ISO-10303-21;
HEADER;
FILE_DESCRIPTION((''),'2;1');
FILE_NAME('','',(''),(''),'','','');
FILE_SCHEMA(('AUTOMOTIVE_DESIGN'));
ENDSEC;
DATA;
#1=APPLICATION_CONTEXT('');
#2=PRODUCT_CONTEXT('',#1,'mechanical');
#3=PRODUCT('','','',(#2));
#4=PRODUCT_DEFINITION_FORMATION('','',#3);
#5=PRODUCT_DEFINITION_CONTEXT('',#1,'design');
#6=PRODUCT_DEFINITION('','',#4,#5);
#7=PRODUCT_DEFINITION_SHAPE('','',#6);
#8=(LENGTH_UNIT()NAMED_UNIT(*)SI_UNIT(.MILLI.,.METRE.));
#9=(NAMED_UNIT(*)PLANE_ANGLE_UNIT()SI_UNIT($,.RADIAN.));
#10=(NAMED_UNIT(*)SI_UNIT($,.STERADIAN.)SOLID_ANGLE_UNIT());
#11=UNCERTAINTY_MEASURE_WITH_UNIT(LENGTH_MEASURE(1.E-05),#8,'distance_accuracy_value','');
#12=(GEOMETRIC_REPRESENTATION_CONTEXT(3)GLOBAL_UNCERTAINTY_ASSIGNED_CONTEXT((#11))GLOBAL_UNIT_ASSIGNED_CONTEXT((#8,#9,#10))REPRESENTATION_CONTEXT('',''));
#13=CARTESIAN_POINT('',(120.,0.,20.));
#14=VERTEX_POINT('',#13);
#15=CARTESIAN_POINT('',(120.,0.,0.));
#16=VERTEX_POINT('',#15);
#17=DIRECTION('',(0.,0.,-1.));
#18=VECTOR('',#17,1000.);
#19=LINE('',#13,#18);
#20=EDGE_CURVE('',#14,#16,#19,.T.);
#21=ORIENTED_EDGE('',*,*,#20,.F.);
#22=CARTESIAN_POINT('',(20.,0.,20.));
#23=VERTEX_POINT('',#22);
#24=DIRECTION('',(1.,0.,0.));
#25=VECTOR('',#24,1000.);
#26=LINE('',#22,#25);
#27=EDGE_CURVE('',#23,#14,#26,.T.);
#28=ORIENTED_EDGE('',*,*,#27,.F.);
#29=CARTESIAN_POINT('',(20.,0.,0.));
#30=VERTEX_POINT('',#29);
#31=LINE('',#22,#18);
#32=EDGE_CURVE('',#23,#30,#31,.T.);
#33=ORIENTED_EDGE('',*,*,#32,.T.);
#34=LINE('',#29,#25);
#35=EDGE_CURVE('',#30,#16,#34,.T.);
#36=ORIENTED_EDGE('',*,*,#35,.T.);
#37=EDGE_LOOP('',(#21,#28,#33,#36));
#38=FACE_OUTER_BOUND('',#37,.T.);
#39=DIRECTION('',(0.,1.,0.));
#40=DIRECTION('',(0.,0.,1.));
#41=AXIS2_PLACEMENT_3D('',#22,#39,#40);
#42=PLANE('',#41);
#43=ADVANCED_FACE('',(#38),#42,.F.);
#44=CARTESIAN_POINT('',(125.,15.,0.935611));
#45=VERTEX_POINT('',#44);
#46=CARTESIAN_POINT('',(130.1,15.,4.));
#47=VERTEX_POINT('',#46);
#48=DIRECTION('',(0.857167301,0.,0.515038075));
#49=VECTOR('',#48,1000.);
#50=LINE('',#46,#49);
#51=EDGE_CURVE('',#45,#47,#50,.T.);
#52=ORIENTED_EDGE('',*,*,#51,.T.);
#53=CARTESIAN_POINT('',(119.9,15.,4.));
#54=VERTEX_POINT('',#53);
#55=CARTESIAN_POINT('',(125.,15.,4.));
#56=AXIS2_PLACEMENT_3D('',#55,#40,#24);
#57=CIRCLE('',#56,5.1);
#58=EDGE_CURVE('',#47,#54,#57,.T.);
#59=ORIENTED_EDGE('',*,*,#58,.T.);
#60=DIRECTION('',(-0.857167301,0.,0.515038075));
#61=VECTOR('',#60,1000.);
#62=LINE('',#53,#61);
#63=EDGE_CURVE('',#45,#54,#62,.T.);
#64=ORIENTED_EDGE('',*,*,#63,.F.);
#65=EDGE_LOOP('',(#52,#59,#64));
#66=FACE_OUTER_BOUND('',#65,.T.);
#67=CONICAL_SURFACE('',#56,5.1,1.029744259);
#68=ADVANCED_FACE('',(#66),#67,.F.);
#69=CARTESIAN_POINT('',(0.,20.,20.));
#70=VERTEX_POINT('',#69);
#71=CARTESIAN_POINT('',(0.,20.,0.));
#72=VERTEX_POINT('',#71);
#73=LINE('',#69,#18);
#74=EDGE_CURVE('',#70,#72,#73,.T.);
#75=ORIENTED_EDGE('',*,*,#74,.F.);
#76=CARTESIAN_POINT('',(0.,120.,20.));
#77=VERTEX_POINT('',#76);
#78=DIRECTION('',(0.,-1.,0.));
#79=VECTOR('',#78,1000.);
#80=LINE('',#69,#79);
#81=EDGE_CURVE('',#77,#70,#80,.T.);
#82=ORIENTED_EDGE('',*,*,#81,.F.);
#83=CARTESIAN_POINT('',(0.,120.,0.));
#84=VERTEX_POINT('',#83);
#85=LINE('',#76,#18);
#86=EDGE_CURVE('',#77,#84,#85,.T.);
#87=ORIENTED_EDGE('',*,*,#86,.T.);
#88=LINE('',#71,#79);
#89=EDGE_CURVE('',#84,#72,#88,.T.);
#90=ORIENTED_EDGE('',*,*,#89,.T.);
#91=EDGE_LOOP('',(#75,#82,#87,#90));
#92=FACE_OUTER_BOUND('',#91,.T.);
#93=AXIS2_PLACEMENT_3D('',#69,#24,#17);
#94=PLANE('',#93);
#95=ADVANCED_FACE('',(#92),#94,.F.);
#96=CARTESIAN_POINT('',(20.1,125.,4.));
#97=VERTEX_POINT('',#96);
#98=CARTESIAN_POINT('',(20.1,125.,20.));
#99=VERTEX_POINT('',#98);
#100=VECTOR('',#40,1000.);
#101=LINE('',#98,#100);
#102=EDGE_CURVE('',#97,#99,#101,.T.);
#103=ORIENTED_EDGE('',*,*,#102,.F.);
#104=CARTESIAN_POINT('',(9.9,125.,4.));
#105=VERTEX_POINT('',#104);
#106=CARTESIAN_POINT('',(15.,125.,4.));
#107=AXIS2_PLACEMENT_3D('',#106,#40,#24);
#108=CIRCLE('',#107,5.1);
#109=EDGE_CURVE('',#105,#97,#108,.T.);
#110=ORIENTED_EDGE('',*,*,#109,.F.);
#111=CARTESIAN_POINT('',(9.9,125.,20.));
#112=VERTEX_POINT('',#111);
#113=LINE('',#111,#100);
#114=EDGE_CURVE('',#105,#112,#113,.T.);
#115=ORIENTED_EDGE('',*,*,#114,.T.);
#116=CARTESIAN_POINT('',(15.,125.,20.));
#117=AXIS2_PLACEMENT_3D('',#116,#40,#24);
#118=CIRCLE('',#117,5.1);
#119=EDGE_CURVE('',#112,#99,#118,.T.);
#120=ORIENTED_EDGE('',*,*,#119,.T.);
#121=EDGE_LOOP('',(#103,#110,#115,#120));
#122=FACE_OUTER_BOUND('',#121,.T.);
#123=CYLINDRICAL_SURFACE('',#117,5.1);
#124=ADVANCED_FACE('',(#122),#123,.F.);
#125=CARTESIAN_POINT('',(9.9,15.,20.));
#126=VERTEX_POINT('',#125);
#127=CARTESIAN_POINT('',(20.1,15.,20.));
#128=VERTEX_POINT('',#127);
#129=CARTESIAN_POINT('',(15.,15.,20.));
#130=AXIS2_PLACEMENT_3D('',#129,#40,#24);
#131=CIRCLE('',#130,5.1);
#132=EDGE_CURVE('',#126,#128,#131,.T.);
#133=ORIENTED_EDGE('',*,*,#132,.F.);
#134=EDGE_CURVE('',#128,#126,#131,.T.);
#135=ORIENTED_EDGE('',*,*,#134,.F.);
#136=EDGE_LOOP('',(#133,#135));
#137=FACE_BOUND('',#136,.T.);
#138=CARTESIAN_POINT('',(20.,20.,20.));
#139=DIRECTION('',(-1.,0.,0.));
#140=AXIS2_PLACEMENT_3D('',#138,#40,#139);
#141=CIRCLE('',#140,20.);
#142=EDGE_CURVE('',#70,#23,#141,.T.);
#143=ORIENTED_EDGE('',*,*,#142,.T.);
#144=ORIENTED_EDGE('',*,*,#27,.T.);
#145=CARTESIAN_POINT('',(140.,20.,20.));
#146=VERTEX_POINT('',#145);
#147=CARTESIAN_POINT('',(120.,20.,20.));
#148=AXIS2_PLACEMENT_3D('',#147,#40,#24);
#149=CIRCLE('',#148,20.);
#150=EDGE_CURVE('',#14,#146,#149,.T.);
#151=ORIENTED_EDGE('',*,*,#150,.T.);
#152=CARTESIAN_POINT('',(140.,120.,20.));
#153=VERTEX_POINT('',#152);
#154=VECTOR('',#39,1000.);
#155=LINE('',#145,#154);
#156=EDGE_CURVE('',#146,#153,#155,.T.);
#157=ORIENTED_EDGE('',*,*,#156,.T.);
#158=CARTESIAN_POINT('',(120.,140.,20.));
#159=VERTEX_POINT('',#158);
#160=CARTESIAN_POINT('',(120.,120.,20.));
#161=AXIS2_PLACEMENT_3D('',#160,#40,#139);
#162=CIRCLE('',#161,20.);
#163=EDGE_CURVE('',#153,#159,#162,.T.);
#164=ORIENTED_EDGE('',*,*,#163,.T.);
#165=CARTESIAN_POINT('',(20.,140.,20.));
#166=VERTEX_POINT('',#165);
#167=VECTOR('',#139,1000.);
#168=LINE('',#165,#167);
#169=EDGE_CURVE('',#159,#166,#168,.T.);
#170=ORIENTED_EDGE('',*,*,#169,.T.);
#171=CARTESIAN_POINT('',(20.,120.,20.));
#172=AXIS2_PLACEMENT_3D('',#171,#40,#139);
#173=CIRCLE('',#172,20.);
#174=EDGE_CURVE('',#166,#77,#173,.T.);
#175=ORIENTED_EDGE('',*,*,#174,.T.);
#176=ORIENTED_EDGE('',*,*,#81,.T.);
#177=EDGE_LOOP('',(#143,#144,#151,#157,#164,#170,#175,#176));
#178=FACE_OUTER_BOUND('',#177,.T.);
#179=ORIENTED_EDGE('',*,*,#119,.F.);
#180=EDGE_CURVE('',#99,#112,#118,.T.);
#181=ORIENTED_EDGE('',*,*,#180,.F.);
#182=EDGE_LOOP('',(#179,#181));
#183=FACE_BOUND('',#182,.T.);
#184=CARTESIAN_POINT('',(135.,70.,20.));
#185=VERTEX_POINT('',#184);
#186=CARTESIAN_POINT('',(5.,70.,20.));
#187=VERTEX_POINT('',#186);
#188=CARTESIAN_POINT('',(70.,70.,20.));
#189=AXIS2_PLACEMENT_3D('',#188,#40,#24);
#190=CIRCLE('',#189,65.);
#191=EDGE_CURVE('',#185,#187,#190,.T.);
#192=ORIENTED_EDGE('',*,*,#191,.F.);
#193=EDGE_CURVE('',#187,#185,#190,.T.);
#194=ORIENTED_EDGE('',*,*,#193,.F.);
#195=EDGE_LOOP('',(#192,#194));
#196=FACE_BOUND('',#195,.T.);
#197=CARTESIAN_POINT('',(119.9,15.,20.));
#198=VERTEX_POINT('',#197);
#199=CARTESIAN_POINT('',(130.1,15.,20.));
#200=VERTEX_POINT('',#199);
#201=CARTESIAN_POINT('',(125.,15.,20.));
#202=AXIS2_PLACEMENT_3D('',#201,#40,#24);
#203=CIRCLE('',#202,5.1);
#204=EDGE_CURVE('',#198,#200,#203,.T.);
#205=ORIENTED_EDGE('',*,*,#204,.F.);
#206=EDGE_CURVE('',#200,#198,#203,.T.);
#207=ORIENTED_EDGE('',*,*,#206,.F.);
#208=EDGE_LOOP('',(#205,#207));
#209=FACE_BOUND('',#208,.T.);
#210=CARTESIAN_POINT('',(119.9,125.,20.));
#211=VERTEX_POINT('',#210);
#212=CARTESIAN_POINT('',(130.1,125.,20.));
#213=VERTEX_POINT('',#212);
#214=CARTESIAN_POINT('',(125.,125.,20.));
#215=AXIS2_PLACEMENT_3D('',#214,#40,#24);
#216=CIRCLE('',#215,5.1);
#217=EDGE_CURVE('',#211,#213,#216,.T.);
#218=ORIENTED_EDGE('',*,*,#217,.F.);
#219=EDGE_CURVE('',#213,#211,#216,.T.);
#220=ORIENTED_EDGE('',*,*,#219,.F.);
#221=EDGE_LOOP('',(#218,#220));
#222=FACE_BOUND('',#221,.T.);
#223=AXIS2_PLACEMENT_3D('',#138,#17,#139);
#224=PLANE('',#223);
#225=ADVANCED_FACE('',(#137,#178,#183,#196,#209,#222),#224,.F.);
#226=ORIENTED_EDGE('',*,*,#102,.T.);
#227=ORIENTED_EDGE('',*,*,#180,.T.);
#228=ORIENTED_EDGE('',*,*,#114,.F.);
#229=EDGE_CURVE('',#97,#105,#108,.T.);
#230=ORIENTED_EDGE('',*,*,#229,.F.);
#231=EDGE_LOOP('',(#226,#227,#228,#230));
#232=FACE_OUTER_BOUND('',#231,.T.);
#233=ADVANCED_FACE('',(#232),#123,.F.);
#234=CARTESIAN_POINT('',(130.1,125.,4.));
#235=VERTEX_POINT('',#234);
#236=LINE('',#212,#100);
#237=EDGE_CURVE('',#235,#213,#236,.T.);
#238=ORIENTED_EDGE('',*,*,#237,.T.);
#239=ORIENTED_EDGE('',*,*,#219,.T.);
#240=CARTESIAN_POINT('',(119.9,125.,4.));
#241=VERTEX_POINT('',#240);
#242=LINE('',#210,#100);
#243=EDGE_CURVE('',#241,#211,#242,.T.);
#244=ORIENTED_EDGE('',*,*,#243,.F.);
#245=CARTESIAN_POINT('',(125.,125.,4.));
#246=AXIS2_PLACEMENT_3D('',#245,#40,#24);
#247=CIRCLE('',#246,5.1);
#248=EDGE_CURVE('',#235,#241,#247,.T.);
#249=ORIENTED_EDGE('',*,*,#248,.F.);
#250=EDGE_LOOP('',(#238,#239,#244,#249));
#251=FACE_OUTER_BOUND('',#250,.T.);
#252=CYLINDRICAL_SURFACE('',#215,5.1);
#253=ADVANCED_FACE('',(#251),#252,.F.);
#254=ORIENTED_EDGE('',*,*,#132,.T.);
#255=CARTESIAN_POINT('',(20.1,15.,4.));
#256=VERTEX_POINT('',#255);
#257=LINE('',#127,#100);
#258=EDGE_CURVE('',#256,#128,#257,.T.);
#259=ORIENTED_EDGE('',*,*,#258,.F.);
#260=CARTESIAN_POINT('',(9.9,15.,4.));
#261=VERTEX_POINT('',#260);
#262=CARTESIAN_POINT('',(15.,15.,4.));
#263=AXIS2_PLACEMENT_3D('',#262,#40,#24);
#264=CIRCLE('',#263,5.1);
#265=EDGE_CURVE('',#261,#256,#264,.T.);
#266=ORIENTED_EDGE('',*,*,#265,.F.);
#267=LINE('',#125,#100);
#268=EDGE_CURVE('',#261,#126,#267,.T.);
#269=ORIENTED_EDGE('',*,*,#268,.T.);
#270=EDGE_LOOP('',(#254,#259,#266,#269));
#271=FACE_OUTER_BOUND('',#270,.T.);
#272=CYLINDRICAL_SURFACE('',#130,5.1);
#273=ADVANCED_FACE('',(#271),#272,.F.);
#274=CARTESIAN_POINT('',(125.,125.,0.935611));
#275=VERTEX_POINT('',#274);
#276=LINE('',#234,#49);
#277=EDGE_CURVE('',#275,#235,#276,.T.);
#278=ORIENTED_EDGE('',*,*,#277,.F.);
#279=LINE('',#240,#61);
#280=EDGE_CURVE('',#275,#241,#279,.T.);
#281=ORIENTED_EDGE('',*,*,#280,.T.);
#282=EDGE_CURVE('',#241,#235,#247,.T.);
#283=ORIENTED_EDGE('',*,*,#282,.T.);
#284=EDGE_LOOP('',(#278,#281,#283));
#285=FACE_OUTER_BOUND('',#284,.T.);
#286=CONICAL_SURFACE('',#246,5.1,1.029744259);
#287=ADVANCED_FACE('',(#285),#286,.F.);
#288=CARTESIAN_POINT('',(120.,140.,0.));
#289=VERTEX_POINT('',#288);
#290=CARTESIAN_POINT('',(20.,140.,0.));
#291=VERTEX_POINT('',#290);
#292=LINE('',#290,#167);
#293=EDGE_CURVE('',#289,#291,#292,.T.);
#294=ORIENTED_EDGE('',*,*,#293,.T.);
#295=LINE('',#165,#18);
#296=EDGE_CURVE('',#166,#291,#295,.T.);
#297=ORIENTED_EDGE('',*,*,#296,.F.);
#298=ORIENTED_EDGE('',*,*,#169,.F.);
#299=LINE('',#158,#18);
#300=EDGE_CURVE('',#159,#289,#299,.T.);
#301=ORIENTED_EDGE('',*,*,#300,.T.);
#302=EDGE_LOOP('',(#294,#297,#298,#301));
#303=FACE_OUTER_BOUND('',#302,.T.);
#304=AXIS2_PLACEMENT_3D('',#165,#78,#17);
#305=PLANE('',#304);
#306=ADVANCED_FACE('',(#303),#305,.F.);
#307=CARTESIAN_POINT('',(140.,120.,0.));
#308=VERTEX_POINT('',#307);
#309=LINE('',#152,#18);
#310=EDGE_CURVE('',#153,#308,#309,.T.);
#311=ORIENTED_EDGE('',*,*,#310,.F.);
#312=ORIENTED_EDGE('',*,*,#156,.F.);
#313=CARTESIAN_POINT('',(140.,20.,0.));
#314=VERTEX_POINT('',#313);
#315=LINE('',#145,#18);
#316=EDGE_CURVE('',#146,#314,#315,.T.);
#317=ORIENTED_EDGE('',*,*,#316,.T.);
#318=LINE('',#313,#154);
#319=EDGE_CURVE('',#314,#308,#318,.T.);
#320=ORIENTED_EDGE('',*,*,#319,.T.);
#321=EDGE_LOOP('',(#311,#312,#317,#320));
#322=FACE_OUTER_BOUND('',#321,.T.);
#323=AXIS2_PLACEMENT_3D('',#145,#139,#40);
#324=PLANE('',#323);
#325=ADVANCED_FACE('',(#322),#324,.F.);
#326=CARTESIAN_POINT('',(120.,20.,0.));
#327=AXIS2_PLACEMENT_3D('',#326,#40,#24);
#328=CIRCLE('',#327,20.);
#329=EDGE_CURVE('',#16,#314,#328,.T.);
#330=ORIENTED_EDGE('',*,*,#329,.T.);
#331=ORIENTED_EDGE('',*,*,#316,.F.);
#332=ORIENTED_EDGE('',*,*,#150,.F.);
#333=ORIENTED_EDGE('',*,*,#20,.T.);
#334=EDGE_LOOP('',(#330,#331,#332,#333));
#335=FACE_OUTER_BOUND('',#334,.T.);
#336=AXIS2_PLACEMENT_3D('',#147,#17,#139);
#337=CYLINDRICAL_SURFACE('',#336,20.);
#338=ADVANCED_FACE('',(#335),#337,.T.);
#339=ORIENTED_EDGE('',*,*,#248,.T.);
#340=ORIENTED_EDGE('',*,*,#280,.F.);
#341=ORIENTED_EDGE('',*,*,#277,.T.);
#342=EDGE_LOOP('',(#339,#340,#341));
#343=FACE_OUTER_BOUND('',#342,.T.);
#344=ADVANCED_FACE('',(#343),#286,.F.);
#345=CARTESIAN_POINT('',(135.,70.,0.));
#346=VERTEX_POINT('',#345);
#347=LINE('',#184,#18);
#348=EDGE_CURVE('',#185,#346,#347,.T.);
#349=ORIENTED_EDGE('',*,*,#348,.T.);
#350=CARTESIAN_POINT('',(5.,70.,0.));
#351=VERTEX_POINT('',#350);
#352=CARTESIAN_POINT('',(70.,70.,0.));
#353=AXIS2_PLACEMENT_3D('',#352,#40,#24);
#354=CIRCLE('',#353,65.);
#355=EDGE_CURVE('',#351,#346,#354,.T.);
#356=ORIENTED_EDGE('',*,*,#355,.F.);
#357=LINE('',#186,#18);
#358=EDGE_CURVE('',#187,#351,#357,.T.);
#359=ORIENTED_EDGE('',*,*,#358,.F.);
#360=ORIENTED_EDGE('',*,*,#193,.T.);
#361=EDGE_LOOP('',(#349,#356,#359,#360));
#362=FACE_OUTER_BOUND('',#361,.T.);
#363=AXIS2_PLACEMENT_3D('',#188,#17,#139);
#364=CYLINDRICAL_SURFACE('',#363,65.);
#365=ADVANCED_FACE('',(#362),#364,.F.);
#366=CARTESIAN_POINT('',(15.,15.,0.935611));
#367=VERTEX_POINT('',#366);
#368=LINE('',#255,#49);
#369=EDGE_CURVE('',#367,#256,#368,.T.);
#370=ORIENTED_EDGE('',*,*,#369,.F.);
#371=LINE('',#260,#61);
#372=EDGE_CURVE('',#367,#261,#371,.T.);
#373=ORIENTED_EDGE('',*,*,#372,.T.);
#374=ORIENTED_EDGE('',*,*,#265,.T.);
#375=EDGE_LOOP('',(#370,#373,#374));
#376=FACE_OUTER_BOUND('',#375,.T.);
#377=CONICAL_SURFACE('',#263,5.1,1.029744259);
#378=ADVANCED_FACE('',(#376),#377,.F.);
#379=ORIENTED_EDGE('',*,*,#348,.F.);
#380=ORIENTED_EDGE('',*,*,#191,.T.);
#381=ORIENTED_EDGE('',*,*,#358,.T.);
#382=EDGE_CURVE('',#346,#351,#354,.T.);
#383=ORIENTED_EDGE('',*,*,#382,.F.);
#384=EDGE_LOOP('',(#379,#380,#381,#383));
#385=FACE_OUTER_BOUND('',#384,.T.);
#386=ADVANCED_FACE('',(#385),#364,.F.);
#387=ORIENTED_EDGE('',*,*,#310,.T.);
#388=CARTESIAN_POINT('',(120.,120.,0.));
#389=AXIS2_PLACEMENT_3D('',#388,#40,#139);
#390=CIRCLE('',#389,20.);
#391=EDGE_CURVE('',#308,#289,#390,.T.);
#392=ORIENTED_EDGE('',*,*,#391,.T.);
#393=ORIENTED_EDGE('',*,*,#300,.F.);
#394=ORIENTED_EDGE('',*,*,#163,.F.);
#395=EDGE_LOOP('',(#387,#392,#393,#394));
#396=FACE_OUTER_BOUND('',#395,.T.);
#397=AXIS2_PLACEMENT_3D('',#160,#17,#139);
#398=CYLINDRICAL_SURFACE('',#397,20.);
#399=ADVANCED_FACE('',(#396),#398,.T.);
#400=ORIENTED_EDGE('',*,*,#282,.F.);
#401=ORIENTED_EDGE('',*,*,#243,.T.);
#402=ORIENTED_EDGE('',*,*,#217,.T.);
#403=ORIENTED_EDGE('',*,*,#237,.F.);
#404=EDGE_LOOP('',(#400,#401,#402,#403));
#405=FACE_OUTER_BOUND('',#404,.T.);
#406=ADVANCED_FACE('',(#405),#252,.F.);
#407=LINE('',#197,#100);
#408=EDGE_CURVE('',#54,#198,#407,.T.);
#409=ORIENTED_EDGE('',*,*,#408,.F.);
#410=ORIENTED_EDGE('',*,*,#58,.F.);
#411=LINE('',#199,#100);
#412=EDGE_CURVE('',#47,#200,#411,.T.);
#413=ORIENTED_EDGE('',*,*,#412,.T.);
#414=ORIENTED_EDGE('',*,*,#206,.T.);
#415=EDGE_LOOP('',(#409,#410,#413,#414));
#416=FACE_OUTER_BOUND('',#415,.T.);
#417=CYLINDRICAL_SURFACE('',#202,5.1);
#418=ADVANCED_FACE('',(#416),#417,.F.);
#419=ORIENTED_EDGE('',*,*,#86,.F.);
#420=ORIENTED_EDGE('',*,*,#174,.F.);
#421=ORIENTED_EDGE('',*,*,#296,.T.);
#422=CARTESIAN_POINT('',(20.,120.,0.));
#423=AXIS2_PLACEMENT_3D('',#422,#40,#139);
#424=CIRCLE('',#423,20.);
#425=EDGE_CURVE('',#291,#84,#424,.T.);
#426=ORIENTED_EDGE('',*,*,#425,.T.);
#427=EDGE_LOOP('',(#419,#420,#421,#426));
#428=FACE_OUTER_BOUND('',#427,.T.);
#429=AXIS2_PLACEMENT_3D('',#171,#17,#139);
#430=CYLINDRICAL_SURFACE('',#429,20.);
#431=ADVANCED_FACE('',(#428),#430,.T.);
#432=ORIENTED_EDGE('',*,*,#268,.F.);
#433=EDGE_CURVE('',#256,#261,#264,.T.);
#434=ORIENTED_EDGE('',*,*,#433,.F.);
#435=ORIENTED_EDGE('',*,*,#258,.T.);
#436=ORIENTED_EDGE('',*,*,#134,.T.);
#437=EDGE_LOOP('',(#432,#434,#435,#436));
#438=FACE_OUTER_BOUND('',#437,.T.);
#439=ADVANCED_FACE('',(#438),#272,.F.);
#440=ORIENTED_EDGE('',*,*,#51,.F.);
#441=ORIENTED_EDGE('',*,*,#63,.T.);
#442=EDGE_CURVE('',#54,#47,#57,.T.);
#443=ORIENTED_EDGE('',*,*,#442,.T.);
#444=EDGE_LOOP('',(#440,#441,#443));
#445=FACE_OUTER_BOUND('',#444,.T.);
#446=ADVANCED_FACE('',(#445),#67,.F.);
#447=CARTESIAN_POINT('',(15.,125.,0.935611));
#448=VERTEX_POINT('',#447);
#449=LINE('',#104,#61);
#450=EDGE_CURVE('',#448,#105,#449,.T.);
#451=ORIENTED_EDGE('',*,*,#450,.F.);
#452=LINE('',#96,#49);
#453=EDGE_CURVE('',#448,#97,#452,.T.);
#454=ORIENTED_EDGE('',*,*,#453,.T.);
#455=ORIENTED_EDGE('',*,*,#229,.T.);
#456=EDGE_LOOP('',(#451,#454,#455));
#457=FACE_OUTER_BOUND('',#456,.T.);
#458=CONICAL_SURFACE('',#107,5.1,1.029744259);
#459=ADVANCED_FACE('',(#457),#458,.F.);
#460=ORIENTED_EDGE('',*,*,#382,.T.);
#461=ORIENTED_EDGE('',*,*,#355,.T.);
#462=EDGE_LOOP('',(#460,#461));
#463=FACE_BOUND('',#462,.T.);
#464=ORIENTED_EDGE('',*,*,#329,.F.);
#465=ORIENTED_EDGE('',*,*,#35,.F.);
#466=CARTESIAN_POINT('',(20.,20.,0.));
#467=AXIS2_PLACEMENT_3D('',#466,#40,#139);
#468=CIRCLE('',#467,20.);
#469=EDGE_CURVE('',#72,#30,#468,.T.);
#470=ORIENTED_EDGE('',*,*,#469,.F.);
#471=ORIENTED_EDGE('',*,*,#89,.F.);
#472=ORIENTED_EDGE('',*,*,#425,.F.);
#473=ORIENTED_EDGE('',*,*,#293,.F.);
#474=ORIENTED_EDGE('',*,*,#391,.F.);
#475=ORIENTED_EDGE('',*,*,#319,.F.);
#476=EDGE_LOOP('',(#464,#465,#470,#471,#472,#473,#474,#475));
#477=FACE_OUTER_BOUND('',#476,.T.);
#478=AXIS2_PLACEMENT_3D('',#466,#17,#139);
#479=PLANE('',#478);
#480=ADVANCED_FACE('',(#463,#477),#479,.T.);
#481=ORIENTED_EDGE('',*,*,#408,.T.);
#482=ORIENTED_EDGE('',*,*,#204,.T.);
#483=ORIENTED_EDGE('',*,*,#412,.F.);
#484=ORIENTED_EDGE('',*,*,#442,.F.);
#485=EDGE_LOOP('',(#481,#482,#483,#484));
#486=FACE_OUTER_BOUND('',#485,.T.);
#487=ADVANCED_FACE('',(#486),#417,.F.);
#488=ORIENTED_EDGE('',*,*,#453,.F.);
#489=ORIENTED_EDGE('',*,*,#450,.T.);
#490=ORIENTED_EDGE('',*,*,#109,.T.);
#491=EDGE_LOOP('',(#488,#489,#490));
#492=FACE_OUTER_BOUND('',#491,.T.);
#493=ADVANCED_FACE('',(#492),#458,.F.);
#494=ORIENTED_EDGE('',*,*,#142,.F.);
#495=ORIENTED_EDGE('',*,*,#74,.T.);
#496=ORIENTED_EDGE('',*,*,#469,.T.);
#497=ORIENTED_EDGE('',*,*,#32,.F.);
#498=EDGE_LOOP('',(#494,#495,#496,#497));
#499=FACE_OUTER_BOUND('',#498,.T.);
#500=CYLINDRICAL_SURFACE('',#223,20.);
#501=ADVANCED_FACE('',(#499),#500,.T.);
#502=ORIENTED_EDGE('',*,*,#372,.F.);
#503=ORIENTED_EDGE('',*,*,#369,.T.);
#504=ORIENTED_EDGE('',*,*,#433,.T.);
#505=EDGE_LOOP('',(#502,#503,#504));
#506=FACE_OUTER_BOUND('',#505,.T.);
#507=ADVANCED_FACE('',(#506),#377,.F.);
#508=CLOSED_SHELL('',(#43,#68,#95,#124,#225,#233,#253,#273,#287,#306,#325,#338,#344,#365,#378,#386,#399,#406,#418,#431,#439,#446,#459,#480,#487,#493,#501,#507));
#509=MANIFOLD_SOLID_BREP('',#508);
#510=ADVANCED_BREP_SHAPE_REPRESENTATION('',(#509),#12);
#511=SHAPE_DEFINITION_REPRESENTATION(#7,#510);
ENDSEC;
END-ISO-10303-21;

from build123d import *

# Parameters (mm, degrees)
SKETCH1_R              = 65
BOSS_EXTRUDE1_DEPTH    = 20
M12_TAPPED_HOLE1_D     = 10.2
M12_TAPPED_HOLE1_DEPTH = 16
M12_TAPPED_HOLE1_TIP   = 3.064389157


with BuildPart() as part:
    # Sketch1 → Boss-Extrude1 (new body)
    with BuildSketch(Plane.XY):
        with BuildLine():
            Line((20, 0), (120, 0))
            ThreePointArc((120, 0), (134.142135624, 5.857864376), (140, 20))
            Line((140, 20), (140, 120))
            ThreePointArc((140, 120), (134.142135624, 134.142135624), (120, 140))
            Line((120, 140), (20, 140))
            ThreePointArc((20, 140), (5.857864376, 134.142135624), (0, 120))
            Line((0, 120), (0, 20))
            ThreePointArc((0, 20), (5.857864376, 5.857864376), (20, 0))
        make_face()
        with Locations((70, 70)):
            Circle(SKETCH1_R, mode=Mode.SUBTRACT)
    extrude(amount=BOSS_EXTRUDE1_DEPTH)

    # M12 Tapped Hole1
    with Locations(Plane(origin=(15, 125, 20), x_dir=(1, 0, 0), z_dir=(0, 0, 1))):
        with Locations((0, 0), (110, 0), (110, -110), (0, -110)):
            Hole(M12_TAPPED_HOLE1_D / 2, depth=M12_TAPPED_HOLE1_DEPTH)
            with Locations((0, 0, -(M12_TAPPED_HOLE1_DEPTH + M12_TAPPED_HOLE1_TIP / 2))):  # 118° drill point
                Cone(0, M12_TAPPED_HOLE1_D / 2, M12_TAPPED_HOLE1_TIP, mode=Mode.SUBTRACT)


solid = part.part
